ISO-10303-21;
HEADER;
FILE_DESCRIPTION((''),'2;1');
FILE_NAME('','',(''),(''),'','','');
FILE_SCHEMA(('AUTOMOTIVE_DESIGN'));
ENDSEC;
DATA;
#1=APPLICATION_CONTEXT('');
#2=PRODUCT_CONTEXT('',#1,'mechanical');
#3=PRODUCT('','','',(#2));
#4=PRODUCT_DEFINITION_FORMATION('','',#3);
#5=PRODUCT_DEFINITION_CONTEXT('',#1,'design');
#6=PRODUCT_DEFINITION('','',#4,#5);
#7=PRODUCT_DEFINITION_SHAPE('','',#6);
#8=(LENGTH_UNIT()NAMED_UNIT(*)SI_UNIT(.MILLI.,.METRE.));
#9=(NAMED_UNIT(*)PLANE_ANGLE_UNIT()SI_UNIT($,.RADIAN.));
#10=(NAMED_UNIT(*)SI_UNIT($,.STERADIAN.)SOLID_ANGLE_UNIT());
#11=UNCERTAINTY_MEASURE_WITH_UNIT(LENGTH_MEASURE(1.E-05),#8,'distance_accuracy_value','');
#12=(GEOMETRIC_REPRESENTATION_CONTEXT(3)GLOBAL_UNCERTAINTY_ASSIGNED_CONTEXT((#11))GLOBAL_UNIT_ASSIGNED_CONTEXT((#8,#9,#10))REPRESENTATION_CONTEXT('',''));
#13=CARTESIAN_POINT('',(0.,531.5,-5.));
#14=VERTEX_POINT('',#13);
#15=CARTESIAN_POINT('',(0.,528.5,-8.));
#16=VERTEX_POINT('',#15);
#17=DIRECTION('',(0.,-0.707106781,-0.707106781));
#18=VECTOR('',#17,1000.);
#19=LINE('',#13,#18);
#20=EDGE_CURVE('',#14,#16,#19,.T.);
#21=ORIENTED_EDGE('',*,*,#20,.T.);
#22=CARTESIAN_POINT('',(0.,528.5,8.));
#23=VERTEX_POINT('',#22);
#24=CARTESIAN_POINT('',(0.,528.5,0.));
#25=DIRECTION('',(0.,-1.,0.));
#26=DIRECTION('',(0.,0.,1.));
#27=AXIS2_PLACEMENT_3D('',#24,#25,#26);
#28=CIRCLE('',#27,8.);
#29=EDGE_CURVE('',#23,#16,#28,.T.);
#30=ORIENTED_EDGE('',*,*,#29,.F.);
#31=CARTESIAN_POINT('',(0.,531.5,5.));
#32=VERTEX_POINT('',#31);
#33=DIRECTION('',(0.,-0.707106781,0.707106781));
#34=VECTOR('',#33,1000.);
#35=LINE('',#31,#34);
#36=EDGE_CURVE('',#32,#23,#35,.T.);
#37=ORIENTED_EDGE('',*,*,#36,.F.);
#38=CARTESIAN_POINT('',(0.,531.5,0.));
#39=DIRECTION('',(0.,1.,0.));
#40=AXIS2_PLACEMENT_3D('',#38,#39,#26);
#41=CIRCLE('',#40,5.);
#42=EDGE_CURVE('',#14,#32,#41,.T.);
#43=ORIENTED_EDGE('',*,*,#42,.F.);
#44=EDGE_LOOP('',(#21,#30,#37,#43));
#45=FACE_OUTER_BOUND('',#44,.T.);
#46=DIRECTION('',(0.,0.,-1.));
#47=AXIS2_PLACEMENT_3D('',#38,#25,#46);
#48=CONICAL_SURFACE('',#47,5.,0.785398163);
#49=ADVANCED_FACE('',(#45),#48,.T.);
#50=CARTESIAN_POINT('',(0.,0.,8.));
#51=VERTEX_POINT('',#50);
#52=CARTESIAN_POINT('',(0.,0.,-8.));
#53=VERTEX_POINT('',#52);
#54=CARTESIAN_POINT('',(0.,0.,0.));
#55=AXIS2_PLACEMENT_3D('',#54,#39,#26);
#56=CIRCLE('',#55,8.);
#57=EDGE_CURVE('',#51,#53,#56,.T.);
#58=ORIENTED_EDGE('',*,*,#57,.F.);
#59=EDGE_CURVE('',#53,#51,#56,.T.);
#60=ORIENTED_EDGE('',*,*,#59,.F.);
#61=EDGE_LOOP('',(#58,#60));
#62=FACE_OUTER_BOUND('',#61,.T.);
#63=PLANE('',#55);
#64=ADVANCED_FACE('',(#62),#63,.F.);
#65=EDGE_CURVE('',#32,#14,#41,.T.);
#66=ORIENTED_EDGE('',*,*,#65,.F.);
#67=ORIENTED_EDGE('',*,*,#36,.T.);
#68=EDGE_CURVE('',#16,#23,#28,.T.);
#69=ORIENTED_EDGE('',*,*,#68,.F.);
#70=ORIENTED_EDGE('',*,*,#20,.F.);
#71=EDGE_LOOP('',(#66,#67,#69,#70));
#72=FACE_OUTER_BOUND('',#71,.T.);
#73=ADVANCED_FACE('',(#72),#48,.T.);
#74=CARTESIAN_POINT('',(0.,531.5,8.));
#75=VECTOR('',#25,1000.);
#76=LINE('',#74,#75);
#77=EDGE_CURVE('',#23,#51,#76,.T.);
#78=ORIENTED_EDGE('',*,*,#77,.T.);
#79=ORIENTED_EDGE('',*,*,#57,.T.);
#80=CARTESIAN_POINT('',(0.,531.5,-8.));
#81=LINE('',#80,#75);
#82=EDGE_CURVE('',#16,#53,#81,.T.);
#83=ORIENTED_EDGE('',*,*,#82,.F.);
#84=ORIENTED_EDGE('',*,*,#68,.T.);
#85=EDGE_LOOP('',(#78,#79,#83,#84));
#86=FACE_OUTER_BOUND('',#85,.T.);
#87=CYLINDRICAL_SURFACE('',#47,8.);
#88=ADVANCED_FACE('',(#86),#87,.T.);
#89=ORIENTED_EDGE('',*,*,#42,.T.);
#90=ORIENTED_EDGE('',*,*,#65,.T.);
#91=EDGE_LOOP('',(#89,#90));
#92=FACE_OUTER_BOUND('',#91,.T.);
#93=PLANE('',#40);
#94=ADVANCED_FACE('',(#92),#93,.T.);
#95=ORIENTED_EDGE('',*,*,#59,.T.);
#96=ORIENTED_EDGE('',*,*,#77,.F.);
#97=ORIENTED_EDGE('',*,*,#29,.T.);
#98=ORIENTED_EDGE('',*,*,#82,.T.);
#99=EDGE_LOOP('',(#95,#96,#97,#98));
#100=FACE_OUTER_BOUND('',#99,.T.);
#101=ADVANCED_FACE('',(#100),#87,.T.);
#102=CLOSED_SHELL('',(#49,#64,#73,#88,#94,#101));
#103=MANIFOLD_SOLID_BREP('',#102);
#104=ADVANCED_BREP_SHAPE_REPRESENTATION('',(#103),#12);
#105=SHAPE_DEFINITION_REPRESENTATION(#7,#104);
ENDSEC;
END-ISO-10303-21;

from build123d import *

# Parameters (mm, degrees)
SKETCH1_R           = 8
BOSS_EXTRUDE1_DEPTH = 531.5
CHAMFER1_SIZE       = 3


with BuildPart() as part:
    # Sketch1 → Boss-Extrude1 (new body)
    with BuildSketch(Plane(origin=(0, 0, 0), x_dir=(1, 0, 0), z_dir=(0, 1, 0))):
        with Locations(Location((0, 0, 0), (0, 0, 270))):
            Circle(SKETCH1_R)
    extrude(amount=BOSS_EXTRUDE1_DEPTH)

    # Chamfer1
    chamfer1_edges = [part.edges().sort_by_distance(p)[0] for p in [
        (0, 531.5, -8),
    ]]
    chamfer(chamfer1_edges, length=CHAMFER1_SIZE)


solid = part.part
